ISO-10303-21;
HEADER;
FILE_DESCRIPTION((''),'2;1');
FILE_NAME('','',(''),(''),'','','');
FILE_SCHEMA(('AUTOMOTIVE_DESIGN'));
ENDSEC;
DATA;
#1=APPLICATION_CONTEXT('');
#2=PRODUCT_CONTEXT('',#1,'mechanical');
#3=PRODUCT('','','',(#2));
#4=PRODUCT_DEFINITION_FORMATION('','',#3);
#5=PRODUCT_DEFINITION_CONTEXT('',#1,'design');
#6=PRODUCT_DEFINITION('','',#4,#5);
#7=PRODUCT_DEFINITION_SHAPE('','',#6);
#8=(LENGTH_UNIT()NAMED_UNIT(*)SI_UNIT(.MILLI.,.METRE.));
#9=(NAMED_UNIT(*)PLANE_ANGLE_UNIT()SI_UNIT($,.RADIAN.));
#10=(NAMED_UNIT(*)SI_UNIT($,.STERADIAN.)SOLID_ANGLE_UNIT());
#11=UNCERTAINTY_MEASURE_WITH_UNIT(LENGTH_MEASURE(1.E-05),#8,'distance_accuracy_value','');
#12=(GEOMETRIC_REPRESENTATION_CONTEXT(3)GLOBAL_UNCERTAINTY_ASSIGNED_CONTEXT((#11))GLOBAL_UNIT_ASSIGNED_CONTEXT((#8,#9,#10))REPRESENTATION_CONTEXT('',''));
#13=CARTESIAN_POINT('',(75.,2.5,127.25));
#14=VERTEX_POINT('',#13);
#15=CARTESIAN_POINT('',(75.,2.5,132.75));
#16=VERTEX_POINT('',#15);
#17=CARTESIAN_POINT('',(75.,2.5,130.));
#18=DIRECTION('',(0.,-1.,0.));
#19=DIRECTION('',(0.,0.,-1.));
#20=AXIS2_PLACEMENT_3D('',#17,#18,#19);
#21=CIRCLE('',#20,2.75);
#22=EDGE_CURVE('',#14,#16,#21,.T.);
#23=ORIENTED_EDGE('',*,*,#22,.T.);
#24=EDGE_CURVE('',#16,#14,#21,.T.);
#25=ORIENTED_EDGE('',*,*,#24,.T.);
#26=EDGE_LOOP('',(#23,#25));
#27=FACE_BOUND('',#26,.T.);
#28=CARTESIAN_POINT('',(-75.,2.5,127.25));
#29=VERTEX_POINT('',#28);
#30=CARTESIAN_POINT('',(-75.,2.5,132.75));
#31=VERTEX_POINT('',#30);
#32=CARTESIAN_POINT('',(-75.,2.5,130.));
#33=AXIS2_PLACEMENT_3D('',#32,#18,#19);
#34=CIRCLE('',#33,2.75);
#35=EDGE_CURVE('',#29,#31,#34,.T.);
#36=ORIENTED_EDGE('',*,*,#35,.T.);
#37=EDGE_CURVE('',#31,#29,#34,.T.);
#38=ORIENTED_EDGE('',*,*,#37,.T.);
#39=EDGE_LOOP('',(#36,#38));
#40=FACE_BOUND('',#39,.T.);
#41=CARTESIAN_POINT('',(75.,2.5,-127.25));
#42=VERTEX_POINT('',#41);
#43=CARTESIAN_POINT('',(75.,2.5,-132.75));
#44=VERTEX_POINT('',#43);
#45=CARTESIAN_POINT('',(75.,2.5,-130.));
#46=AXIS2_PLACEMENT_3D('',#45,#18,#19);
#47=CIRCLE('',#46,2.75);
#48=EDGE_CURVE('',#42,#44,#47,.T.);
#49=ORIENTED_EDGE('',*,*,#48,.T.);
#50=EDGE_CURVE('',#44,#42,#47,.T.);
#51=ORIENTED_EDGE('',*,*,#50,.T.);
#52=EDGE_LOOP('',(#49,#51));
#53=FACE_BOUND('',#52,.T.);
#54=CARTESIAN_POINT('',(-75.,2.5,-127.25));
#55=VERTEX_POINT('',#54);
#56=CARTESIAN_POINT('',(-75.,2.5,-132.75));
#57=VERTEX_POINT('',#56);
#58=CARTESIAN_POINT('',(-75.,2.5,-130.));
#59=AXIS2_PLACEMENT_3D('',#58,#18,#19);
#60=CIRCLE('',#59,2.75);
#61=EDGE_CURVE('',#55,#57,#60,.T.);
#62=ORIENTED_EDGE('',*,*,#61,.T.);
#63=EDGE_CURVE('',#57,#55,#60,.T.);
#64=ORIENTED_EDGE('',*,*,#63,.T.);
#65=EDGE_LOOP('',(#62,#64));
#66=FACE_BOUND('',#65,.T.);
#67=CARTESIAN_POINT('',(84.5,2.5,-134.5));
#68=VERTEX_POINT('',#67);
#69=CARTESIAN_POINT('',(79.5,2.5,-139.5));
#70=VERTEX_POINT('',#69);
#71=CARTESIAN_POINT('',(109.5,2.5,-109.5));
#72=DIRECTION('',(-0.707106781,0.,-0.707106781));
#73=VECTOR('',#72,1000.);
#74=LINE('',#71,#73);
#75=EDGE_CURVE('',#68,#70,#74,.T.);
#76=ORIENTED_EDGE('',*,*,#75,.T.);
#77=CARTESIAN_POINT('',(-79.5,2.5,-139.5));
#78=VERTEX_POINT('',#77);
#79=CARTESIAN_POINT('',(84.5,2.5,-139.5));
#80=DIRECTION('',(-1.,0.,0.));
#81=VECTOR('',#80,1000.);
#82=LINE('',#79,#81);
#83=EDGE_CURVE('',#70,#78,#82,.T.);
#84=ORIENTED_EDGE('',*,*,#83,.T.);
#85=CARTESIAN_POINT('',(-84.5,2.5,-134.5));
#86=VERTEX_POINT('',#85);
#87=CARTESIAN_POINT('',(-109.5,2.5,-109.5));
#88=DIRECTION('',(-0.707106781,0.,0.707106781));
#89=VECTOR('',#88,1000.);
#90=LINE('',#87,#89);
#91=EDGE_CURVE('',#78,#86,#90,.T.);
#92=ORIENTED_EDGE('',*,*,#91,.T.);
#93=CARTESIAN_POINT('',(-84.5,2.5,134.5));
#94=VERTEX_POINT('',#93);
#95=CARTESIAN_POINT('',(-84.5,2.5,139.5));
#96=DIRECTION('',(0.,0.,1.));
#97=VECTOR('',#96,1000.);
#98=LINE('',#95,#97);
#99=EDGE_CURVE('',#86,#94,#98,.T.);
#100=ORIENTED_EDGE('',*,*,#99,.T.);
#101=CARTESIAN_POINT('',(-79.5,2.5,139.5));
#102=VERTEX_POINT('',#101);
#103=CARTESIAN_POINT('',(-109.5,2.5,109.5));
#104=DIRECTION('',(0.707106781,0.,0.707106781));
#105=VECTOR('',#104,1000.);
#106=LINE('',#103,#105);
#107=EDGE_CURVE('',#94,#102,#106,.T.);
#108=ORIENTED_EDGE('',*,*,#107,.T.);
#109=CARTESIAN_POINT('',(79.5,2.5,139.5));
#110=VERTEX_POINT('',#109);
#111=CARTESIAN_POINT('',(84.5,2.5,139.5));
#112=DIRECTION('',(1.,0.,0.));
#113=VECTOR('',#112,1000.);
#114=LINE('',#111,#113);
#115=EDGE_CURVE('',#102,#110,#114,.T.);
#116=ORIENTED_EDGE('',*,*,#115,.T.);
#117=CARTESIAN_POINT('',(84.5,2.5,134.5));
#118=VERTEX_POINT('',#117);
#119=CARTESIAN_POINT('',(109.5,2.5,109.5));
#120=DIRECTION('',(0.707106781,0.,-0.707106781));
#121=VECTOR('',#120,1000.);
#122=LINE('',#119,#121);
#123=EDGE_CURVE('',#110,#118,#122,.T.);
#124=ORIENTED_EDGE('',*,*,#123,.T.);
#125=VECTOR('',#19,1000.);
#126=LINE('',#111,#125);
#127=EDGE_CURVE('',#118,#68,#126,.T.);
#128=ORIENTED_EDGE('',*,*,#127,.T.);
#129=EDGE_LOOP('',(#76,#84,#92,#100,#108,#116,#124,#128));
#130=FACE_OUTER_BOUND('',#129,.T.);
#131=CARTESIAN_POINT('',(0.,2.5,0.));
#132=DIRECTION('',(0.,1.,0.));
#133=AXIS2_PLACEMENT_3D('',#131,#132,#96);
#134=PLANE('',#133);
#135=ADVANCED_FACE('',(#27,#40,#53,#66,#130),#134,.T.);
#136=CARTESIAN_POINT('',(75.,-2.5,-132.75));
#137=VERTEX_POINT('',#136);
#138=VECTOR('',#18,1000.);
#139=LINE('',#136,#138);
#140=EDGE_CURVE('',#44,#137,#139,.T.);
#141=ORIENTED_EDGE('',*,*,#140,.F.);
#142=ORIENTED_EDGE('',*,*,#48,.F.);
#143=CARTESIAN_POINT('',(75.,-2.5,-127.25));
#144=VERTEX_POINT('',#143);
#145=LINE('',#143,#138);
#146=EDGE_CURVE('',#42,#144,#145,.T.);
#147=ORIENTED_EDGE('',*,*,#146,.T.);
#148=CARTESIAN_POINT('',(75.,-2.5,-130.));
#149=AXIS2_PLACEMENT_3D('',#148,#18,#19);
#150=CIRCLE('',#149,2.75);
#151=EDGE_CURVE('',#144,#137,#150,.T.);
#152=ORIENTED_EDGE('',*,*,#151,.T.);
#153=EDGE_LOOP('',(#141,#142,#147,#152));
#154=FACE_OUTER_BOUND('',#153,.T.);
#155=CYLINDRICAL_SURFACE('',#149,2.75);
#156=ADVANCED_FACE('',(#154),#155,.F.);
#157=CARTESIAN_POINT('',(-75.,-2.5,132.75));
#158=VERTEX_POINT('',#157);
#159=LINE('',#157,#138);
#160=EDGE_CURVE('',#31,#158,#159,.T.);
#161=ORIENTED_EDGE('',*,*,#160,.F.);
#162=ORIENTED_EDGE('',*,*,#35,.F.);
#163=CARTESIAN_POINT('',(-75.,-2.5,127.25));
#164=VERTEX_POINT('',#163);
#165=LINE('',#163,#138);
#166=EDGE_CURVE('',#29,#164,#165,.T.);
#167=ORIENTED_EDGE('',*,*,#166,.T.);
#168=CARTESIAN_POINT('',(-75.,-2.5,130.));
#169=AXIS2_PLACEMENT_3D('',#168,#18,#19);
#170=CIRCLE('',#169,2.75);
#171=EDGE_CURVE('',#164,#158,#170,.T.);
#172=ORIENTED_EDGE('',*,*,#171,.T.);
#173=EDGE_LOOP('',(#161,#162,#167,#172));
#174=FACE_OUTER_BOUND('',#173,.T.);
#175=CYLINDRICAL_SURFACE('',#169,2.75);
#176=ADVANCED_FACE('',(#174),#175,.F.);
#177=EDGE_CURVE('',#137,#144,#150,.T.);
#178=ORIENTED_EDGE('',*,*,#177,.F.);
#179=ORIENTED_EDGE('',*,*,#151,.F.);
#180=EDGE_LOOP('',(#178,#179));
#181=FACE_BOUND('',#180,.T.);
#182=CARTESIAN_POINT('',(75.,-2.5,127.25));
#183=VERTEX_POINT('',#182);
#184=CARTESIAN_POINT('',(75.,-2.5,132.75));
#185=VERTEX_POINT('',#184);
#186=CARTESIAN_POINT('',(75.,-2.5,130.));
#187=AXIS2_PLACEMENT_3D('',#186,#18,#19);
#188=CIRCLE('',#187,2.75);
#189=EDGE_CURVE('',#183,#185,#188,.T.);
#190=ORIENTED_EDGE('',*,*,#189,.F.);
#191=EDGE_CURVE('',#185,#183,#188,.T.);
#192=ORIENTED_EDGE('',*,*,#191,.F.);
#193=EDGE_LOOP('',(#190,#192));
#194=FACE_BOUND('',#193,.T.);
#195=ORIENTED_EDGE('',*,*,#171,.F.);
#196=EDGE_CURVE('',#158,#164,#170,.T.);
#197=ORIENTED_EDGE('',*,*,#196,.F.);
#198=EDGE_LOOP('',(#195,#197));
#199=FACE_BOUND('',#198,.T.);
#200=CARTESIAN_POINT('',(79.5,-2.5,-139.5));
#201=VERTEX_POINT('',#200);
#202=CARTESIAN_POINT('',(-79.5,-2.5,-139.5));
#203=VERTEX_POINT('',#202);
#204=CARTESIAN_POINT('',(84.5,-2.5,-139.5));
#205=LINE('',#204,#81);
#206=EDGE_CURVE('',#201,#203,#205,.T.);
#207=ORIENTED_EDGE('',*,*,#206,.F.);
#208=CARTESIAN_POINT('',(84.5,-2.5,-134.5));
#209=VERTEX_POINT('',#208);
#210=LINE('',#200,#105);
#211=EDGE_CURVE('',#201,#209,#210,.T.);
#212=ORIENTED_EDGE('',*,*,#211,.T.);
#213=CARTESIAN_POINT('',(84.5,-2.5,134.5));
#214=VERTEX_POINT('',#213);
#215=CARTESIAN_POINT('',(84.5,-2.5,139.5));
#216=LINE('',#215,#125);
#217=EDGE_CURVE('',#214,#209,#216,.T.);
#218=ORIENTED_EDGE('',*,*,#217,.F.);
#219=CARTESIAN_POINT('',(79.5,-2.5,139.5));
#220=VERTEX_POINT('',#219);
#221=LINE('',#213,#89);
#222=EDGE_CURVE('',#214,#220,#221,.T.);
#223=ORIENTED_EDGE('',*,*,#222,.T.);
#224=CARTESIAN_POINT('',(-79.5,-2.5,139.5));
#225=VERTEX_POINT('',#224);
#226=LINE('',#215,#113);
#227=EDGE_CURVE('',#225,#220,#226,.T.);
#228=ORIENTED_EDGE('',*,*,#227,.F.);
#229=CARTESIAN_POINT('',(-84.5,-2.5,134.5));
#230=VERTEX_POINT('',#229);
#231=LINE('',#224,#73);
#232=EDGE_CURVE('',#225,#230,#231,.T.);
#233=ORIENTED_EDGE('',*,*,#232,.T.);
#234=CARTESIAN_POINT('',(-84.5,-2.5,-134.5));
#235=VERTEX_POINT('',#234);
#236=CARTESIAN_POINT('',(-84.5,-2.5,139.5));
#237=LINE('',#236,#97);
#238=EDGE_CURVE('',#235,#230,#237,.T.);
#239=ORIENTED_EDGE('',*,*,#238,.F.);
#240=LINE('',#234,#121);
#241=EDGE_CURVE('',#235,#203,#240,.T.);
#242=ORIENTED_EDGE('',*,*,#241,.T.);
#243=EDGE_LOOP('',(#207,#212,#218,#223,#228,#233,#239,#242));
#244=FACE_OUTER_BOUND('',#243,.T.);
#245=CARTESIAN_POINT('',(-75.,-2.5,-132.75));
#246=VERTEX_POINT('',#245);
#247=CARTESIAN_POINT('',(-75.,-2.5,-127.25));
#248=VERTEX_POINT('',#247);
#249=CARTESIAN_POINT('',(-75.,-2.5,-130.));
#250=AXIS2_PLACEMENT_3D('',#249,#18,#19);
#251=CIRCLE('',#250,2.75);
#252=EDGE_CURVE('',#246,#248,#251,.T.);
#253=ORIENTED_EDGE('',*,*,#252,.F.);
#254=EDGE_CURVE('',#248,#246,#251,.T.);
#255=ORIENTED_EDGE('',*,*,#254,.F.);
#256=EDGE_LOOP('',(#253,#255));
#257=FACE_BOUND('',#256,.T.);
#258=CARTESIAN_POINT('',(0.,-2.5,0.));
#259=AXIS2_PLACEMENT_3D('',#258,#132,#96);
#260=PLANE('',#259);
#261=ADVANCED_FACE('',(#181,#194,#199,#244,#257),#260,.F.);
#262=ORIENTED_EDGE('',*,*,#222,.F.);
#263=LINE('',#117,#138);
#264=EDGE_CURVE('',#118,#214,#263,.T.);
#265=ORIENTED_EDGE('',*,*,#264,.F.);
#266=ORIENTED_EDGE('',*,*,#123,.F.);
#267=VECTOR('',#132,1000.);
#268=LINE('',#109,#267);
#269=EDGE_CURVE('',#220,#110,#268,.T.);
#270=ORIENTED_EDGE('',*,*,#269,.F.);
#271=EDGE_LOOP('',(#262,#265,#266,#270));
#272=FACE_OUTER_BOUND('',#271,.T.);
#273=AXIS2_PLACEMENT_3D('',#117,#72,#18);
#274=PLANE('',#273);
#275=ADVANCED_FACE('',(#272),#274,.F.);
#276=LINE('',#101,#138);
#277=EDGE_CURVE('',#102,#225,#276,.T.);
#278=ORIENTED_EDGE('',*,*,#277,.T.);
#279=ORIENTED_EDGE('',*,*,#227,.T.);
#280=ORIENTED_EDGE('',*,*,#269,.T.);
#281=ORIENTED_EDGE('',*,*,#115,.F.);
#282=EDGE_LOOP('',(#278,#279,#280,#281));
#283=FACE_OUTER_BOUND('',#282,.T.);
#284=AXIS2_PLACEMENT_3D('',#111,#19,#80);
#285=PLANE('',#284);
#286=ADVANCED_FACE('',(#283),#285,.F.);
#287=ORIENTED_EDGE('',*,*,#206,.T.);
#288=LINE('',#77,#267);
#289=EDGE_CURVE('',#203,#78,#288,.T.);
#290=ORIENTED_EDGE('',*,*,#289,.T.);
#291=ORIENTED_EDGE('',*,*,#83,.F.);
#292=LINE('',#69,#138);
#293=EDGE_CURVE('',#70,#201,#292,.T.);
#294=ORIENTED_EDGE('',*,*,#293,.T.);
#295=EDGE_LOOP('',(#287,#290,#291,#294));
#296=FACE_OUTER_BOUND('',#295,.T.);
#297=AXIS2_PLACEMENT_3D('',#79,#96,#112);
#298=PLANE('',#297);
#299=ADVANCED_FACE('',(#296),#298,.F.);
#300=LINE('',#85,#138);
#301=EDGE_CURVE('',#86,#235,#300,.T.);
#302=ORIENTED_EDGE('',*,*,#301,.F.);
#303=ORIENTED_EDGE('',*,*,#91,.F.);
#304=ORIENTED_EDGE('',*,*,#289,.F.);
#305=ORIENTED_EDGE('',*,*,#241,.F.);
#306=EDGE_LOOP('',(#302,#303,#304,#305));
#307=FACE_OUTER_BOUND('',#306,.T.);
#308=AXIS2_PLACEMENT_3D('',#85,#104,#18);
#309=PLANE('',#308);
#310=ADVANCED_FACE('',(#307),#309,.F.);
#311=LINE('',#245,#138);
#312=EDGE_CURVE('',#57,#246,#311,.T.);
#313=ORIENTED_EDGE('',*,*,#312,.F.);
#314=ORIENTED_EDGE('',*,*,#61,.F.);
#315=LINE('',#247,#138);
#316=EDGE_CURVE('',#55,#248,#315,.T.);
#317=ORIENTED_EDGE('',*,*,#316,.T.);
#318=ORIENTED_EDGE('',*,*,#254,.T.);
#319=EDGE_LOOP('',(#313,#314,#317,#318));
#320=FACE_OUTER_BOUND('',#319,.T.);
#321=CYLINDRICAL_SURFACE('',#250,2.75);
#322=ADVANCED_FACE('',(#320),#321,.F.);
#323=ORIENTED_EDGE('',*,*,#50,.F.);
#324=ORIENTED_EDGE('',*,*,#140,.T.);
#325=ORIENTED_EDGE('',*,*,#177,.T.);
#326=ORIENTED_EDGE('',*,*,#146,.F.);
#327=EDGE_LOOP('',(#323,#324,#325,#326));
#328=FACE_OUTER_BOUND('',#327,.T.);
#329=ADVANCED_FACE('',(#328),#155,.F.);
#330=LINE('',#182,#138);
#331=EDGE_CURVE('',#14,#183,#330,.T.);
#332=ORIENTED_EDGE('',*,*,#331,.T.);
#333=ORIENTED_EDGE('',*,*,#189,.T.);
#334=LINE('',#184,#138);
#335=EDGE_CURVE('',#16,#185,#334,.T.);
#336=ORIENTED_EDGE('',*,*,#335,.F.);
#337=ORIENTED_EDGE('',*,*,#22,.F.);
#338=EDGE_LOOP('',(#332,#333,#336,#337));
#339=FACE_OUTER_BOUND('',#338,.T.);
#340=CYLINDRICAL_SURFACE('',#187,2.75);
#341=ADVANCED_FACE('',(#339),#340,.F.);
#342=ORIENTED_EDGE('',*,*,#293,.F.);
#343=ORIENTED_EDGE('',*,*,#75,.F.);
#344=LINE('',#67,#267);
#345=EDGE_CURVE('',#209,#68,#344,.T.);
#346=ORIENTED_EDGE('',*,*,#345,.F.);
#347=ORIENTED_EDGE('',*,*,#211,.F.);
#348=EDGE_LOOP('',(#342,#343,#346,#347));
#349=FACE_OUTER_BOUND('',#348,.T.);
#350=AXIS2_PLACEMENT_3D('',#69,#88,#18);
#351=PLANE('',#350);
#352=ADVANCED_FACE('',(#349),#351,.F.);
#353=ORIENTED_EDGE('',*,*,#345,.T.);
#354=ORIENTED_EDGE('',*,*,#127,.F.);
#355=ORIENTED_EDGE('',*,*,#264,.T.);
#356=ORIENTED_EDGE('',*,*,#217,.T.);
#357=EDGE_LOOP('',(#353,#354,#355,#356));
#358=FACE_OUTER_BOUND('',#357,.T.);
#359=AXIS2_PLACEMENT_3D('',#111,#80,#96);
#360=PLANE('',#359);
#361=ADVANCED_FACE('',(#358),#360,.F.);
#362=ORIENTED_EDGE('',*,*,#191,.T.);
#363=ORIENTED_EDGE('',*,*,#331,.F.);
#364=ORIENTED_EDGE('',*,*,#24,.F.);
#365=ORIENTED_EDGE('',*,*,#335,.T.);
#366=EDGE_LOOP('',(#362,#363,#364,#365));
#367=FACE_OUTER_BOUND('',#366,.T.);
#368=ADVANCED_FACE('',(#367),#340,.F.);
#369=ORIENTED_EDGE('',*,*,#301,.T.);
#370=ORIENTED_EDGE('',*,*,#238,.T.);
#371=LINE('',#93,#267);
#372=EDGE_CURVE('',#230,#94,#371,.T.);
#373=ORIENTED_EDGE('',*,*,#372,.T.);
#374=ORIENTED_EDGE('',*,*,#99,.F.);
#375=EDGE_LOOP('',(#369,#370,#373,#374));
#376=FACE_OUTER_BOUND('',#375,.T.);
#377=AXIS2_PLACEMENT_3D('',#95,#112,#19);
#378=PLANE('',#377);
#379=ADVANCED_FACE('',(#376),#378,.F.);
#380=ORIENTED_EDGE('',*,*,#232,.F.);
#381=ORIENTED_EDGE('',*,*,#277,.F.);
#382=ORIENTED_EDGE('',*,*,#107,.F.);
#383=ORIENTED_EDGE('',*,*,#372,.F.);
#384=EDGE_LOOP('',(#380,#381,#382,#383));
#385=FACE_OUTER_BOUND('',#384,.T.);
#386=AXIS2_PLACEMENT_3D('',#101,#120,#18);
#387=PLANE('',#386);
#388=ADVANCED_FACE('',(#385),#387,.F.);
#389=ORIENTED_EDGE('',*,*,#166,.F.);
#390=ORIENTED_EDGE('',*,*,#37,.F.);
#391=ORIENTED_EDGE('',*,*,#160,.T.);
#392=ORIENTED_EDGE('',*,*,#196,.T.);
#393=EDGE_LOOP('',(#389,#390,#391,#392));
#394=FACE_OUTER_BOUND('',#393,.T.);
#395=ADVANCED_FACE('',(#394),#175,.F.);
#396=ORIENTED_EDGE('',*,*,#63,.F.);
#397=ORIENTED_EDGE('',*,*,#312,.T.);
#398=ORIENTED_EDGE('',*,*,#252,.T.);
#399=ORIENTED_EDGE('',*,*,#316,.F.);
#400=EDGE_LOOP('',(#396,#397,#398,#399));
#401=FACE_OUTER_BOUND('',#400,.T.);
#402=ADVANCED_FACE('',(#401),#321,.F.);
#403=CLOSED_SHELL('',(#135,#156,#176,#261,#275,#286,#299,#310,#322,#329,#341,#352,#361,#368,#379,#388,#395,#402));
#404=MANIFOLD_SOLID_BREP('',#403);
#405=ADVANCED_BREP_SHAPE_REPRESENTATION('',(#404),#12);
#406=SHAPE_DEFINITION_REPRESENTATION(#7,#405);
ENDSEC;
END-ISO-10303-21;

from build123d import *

# Parameters (mm, degrees)
SKETCH_1_W              = 169
SKETCH_1_H              = 279
EXTRUDE_1_DEPTH         = 2.5
HOLE_WIZARD_5_5_5_5_1_D = 5.5
CHAMFER_1_SIZE          = 5


with BuildPart() as part:
    # 草图1 → 凸台-拉伸1 (new, symmetric)
    with BuildSketch(Plane(origin=(0, 0, 0), x_dir=(1, 0, 0), z_dir=(0, 1, 0))):
        Rectangle(SKETCH_1_W, SKETCH_1_H)
    extrude(amount=EXTRUDE_1_DEPTH, both=True)

    # Ø5.5 (5.5) 直径孔1 (through all)
    with Locations(Plane(origin=(0, -2.5, 0), x_dir=(-1, 0, 0), z_dir=(0, -1, 0))):
        with Locations((75, -130), (-75, -130), (-75, 130), (75, 130)):
            Hole(HOLE_WIZARD_5_5_5_5_1_D / 2)

    # 倒角1
    chamfer_1_edges = [part.edges().sort_by_distance(p)[0] for p in [
        (-84.5, 0, -139.5),
        (84.5, 0, -139.5),
        (84.5, 0, 139.5),
        (-84.5, 0, 139.5),
    ]]
    chamfer(chamfer_1_edges, length=CHAMFER_1_SIZE)


solid = part.part
